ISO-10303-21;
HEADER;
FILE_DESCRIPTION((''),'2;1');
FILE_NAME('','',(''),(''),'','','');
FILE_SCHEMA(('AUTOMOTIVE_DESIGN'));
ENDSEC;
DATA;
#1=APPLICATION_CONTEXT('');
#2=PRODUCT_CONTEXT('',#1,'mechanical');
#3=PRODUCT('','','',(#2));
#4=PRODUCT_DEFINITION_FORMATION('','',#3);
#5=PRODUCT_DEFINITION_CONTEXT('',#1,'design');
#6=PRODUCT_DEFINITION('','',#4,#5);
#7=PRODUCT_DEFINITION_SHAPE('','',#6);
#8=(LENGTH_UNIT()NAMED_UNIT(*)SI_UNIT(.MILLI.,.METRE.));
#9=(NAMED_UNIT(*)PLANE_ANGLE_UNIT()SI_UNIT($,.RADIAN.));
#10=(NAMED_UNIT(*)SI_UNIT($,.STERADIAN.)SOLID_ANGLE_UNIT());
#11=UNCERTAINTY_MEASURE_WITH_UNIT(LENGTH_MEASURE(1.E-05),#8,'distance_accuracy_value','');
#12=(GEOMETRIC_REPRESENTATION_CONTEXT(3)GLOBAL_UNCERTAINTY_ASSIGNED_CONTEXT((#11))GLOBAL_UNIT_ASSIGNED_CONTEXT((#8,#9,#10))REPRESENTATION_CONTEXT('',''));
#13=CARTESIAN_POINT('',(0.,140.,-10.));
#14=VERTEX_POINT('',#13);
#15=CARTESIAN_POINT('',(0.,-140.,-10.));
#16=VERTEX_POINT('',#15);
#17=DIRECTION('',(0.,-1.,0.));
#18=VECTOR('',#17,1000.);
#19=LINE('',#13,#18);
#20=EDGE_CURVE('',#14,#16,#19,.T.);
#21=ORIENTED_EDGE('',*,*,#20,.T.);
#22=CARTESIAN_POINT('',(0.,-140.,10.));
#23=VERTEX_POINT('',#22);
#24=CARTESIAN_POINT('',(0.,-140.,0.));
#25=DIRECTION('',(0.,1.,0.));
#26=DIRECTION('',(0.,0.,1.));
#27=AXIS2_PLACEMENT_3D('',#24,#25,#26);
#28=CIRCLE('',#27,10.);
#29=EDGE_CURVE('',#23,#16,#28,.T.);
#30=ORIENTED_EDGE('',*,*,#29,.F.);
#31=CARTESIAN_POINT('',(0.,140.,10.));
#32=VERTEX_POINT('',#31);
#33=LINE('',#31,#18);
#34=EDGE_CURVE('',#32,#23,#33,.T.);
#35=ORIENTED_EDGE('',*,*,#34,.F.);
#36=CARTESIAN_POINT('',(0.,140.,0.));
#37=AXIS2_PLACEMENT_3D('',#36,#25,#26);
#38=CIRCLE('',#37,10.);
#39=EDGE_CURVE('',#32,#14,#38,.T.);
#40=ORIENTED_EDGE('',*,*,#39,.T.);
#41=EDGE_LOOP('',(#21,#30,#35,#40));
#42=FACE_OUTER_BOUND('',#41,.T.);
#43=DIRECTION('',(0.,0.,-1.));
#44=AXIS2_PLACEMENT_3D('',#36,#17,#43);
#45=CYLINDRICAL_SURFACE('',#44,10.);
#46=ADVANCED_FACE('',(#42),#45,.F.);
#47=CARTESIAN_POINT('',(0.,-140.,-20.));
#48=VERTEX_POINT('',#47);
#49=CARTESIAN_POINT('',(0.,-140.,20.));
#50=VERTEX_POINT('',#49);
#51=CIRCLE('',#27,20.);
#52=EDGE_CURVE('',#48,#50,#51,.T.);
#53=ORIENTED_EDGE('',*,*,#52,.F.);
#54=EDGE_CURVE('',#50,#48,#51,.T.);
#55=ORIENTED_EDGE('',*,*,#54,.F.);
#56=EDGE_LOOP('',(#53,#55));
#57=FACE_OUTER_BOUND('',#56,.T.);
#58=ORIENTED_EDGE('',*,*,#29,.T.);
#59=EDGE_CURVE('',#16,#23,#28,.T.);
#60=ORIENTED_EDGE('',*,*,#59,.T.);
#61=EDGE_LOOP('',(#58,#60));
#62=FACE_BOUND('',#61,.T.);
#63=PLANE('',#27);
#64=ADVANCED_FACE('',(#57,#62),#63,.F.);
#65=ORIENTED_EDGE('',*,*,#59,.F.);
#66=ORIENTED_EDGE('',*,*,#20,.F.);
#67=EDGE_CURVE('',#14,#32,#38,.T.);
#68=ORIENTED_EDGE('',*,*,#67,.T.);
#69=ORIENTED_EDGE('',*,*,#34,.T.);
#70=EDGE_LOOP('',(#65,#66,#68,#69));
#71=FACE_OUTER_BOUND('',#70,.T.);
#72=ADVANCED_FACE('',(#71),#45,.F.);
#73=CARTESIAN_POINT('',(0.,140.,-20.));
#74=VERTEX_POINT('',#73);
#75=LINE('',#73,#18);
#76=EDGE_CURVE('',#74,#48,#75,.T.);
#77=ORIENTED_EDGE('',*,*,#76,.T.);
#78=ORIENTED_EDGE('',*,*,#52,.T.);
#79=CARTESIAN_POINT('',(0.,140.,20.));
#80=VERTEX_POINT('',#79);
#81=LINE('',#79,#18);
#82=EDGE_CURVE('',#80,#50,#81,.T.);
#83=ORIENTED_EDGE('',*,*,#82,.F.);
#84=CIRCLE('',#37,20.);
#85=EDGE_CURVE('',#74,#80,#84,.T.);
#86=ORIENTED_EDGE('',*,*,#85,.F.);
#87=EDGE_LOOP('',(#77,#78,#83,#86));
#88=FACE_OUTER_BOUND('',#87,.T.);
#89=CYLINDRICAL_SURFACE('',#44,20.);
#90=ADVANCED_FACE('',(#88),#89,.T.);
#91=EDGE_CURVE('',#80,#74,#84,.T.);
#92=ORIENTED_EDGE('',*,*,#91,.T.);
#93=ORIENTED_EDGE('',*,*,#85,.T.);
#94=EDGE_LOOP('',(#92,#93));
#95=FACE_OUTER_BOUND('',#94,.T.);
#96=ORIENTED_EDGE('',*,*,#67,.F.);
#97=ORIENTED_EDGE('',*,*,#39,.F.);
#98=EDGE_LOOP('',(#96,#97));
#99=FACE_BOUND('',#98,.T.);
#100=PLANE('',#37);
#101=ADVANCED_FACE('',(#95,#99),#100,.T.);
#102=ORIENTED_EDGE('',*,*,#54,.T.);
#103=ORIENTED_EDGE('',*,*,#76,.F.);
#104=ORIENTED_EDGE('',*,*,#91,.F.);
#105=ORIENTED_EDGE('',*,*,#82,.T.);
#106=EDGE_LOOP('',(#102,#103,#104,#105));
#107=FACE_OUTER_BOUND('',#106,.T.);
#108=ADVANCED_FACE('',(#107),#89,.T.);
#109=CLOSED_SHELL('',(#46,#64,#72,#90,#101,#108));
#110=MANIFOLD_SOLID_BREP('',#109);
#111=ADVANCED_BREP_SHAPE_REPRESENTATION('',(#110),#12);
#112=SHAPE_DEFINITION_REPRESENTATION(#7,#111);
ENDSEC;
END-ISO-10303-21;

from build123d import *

# Parameters (mm, degrees)
SKETCH1_R           = 20
SKETCH1_R_2         = 10
BOSS_EXTRUDE1_DEPTH = 140


with BuildPart() as part:
    # Sketch1 → Boss-Extrude1 (new, symmetric)
    with BuildSketch(Plane(origin=(0, 0, 0), x_dir=(1, 0, 0), z_dir=(0, 1, 0))):
        with Locations(Location((0, 0, 0), (0, 0, 270))):
            Circle(SKETCH1_R)
        with Locations(Location((0, 0, 0), (0, 0, 270))):
            Circle(SKETCH1_R_2, mode=Mode.SUBTRACT)
    extrude(amount=BOSS_EXTRUDE1_DEPTH, both=True)


solid = part.part
